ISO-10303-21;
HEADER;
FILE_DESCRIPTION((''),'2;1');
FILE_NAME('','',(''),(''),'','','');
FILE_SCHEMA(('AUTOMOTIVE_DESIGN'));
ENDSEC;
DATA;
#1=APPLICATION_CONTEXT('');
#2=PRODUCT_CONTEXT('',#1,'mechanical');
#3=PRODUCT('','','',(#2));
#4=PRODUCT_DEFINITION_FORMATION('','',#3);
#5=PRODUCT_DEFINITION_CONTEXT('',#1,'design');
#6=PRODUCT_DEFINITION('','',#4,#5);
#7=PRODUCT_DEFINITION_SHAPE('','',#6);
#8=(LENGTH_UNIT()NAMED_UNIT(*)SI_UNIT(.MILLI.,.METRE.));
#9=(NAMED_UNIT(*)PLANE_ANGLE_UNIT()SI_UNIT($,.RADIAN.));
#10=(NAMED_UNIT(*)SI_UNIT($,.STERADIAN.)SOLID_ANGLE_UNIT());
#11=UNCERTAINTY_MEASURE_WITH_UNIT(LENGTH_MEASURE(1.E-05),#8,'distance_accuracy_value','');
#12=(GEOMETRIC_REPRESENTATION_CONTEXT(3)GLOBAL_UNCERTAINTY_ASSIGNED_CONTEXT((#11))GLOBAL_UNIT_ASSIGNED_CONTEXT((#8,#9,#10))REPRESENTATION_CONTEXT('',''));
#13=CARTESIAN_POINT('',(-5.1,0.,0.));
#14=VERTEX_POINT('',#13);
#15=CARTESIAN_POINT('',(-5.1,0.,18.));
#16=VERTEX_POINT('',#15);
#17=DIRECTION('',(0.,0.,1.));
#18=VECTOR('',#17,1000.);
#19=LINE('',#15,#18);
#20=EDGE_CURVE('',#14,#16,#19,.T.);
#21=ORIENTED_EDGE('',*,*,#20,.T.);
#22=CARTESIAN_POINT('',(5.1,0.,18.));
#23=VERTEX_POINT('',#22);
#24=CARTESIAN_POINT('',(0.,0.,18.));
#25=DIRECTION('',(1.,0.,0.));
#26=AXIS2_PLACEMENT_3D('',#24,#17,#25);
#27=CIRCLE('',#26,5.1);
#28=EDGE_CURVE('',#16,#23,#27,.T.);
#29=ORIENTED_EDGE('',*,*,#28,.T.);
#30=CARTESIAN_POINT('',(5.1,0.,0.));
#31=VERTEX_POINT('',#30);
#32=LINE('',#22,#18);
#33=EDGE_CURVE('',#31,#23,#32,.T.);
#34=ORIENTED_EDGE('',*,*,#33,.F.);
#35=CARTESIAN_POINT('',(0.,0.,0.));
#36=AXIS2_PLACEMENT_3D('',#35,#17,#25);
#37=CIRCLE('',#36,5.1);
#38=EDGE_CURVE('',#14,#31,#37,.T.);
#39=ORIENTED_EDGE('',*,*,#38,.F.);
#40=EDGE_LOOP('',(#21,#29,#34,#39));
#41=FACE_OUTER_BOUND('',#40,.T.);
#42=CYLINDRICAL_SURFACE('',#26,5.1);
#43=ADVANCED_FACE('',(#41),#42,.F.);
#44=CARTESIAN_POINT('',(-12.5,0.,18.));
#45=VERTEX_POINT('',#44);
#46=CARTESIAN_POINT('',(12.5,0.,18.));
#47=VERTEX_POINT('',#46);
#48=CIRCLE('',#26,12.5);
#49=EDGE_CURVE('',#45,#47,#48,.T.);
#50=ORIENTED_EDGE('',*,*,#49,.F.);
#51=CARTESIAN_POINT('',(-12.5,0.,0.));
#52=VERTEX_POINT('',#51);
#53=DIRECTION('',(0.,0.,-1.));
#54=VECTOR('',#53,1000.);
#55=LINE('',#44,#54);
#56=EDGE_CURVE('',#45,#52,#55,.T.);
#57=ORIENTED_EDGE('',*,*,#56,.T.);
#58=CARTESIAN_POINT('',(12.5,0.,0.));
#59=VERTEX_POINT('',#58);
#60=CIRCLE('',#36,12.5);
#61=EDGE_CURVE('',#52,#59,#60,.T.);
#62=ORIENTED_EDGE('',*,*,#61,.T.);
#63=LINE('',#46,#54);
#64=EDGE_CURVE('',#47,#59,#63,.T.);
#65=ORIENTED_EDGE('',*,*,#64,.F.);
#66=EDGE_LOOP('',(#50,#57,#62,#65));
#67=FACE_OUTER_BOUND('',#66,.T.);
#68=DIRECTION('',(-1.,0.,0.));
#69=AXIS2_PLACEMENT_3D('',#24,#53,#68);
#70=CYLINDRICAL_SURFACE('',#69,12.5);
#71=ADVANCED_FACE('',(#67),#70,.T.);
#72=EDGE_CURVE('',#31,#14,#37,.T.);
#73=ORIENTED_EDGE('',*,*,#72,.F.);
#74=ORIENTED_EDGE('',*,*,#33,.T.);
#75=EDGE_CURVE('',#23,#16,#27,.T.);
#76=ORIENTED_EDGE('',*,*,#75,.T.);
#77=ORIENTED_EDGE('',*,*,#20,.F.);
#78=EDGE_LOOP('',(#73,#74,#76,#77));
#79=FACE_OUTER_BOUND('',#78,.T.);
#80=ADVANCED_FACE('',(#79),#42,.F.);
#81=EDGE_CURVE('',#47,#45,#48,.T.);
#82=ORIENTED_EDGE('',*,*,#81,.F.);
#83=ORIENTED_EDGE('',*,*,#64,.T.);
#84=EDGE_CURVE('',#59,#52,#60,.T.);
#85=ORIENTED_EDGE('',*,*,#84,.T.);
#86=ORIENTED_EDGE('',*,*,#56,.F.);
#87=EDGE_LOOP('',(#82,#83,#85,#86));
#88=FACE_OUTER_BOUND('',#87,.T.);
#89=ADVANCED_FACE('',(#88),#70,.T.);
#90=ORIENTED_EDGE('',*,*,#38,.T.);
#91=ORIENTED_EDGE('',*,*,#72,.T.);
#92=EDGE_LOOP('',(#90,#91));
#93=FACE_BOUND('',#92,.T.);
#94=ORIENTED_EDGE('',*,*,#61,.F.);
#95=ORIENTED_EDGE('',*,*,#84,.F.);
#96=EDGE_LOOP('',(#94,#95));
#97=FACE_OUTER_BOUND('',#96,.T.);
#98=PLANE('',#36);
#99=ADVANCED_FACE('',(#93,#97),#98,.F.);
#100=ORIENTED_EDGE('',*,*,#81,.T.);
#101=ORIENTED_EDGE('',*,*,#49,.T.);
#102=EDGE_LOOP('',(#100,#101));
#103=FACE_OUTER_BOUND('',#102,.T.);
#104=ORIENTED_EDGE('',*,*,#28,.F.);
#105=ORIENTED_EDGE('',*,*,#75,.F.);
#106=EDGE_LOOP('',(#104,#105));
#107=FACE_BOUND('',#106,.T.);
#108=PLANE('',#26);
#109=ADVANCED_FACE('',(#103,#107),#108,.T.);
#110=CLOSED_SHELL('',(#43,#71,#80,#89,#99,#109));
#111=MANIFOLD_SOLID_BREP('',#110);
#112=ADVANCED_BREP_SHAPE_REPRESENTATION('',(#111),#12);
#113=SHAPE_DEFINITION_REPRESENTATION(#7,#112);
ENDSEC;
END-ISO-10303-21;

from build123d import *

# Parameters (mm, degrees)
SKETCH1_R              = 12.5
BOSS_EXTRUDE1_DEPTH    = 18
M12_TAPPED_HOLE1_D     = 10.2
M12_TAPPED_HOLE1_DEPTH = 29.25
M12_TAPPED_HOLE1_TIP   = 3.064389157


with BuildPart() as part:
    # Sketch1 → Boss-Extrude1 (new body)
    with BuildSketch(Plane.XY):
        Circle(SKETCH1_R)
    extrude(amount=BOSS_EXTRUDE1_DEPTH)

    # M12 Tapped Hole1
    with Locations(Plane.XY.offset(18)):
        with Locations((0, 0)):
            Hole(M12_TAPPED_HOLE1_D / 2, depth=M12_TAPPED_HOLE1_DEPTH)
            with Locations((0, 0, -(M12_TAPPED_HOLE1_DEPTH + M12_TAPPED_HOLE1_TIP / 2))):  # 118° drill point
                Cone(0, M12_TAPPED_HOLE1_D / 2, M12_TAPPED_HOLE1_TIP, mode=Mode.SUBTRACT)


solid = part.part
